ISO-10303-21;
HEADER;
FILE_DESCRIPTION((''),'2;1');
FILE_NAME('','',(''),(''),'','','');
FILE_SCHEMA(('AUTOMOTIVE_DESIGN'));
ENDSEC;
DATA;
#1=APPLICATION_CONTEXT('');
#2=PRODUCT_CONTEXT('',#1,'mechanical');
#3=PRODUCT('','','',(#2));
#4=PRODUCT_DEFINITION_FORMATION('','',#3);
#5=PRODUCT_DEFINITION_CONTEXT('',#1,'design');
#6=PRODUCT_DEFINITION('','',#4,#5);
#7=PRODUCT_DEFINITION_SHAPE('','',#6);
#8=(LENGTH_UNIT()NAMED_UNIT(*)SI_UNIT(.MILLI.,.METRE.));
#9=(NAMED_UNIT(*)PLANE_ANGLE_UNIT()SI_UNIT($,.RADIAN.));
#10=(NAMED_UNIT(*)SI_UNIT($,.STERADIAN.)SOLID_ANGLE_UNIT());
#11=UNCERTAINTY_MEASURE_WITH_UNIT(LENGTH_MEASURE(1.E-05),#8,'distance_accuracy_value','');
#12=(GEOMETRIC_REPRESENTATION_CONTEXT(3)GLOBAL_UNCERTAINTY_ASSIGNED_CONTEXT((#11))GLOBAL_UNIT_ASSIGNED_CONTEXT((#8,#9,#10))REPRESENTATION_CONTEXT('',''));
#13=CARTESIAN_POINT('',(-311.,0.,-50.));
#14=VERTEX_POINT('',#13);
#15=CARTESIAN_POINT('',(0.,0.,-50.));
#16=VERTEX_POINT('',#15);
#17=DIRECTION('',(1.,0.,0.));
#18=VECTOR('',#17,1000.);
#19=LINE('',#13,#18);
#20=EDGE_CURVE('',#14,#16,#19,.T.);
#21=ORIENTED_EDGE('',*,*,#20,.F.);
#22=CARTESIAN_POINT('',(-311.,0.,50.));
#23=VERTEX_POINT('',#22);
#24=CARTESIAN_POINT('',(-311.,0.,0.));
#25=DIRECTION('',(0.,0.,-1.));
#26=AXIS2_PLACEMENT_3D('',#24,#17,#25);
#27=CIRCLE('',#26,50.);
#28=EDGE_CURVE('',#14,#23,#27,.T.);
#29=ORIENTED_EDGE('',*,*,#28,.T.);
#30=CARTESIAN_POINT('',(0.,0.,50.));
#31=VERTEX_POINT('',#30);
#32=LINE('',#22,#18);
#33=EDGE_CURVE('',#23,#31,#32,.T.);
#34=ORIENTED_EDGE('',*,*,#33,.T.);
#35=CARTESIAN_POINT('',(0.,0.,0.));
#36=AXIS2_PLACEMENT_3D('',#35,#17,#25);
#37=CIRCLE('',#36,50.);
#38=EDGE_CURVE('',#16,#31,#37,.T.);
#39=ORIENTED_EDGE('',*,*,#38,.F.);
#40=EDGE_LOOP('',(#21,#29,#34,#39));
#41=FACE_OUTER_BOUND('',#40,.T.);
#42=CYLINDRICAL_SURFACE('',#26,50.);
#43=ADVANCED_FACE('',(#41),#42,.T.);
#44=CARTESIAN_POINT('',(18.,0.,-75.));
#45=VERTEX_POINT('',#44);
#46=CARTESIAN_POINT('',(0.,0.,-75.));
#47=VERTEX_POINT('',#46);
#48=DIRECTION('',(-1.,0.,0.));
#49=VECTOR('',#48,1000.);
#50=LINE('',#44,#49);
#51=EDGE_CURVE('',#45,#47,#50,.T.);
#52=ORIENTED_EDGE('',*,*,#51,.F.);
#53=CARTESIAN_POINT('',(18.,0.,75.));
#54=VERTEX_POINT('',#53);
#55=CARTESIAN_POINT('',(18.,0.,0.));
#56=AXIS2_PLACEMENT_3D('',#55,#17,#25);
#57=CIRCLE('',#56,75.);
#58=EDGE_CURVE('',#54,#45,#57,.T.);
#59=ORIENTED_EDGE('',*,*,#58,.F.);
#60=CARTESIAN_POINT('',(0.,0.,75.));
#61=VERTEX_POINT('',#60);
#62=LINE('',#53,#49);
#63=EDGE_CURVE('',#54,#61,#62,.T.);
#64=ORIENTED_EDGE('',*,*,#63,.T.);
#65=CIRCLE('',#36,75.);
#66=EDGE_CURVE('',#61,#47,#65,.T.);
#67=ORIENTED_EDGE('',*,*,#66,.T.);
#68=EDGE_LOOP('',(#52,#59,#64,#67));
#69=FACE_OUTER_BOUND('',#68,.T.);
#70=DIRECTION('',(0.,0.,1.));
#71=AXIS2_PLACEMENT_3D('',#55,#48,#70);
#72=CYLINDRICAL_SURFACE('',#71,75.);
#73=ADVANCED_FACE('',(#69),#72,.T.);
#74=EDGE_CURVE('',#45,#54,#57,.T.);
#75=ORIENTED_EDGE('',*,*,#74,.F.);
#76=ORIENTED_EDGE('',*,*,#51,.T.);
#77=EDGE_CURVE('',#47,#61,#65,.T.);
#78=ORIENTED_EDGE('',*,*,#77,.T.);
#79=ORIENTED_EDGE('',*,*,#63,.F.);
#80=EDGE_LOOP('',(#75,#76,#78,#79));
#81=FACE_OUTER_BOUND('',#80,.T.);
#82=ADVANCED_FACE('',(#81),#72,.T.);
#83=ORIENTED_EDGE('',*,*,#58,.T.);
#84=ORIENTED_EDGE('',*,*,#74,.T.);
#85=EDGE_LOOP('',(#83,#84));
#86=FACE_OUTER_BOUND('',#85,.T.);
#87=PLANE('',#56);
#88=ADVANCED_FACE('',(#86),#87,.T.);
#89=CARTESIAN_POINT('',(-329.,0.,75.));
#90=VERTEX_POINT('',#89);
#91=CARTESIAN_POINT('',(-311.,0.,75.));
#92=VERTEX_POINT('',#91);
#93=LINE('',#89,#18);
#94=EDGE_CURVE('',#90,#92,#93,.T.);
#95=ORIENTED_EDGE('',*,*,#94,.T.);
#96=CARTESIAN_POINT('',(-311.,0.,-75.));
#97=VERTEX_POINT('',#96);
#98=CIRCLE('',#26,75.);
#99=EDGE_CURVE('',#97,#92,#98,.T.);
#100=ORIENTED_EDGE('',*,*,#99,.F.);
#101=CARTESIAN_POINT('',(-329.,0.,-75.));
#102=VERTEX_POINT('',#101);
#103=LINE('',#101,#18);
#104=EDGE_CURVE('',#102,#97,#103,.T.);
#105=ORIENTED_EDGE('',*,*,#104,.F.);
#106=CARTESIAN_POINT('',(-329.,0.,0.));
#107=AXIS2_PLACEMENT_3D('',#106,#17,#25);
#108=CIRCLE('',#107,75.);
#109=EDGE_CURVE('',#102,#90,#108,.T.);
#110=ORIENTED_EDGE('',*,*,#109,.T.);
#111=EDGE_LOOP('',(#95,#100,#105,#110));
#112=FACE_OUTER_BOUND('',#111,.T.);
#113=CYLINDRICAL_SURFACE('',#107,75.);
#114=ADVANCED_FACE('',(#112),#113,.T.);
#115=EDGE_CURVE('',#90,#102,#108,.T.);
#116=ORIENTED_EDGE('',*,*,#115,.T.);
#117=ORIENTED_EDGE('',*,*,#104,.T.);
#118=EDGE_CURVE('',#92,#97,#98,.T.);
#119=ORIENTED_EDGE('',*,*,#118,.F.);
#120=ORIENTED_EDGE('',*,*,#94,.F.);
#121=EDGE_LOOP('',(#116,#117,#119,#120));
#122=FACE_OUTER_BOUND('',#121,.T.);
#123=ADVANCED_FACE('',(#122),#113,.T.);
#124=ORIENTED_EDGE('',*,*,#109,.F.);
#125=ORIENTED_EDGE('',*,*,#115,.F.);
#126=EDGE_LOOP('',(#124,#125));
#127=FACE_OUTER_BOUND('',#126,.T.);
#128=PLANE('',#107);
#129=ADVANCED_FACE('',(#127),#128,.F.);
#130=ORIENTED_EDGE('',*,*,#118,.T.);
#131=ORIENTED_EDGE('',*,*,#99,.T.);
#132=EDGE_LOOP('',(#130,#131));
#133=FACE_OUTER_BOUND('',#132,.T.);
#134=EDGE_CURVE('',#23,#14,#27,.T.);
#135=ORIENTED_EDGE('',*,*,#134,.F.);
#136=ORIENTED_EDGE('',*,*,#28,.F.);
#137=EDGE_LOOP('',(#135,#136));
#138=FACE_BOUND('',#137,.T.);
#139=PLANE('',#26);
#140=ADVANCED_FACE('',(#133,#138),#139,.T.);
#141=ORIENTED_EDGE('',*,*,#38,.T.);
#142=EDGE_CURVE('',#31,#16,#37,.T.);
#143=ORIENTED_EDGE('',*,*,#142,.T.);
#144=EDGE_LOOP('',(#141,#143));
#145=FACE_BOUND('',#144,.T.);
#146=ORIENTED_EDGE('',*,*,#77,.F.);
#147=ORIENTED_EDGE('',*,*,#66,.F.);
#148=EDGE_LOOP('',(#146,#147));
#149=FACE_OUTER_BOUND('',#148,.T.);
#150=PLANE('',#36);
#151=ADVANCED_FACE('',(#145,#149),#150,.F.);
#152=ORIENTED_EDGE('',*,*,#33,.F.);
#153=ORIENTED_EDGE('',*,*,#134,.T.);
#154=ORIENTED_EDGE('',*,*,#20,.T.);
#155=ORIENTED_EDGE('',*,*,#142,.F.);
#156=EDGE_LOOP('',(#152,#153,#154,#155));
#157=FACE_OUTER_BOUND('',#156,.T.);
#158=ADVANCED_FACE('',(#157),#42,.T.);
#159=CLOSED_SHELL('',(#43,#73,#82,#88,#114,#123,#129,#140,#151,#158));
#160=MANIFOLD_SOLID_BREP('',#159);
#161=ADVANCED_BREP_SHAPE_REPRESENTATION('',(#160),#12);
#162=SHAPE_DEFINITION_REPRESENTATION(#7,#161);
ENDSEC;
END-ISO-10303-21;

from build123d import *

# Parameters (mm, degrees)
SKETCH_1_4_R        = 75
BOSS_EXTRUDE1_DEPTH = 18
SKETCH_1_3_R        = 50
BOSS_EXTRUDE2_DEPTH = 311
BOSS_EXTRUDE3_START = -329
SKETCH_1_4_2_R      = 75
BOSS_EXTRUDE3_DEPTH = 18


with BuildPart() as part:
    # Sketch 1_4 → Boss-Extrude1 (new body)
    with BuildSketch(Plane(origin=(0, 0, 0), x_dir=(0, 0, -1), z_dir=(1, 0, 0))):
        Circle(SKETCH_1_4_R)
    extrude(amount=BOSS_EXTRUDE1_DEPTH)

    # 草图1<3> → Boss-Extrude2 (add)
    with BuildSketch(Plane(origin=(0, 0, 0), x_dir=(0, 0, -1), z_dir=(1, 0, 0))):
        Circle(SKETCH_1_3_R)
    extrude(amount=-BOSS_EXTRUDE2_DEPTH)

    # Sketch 1_4 2 → Boss-Extrude3 (add)
    with BuildSketch(Plane(origin=(0, 0, 0), x_dir=(0, 0, -1), z_dir=(1, 0, 0)).offset(BOSS_EXTRUDE3_START)):
        Circle(SKETCH_1_4_2_R)
    extrude(amount=BOSS_EXTRUDE3_DEPTH)


solid = part.part
